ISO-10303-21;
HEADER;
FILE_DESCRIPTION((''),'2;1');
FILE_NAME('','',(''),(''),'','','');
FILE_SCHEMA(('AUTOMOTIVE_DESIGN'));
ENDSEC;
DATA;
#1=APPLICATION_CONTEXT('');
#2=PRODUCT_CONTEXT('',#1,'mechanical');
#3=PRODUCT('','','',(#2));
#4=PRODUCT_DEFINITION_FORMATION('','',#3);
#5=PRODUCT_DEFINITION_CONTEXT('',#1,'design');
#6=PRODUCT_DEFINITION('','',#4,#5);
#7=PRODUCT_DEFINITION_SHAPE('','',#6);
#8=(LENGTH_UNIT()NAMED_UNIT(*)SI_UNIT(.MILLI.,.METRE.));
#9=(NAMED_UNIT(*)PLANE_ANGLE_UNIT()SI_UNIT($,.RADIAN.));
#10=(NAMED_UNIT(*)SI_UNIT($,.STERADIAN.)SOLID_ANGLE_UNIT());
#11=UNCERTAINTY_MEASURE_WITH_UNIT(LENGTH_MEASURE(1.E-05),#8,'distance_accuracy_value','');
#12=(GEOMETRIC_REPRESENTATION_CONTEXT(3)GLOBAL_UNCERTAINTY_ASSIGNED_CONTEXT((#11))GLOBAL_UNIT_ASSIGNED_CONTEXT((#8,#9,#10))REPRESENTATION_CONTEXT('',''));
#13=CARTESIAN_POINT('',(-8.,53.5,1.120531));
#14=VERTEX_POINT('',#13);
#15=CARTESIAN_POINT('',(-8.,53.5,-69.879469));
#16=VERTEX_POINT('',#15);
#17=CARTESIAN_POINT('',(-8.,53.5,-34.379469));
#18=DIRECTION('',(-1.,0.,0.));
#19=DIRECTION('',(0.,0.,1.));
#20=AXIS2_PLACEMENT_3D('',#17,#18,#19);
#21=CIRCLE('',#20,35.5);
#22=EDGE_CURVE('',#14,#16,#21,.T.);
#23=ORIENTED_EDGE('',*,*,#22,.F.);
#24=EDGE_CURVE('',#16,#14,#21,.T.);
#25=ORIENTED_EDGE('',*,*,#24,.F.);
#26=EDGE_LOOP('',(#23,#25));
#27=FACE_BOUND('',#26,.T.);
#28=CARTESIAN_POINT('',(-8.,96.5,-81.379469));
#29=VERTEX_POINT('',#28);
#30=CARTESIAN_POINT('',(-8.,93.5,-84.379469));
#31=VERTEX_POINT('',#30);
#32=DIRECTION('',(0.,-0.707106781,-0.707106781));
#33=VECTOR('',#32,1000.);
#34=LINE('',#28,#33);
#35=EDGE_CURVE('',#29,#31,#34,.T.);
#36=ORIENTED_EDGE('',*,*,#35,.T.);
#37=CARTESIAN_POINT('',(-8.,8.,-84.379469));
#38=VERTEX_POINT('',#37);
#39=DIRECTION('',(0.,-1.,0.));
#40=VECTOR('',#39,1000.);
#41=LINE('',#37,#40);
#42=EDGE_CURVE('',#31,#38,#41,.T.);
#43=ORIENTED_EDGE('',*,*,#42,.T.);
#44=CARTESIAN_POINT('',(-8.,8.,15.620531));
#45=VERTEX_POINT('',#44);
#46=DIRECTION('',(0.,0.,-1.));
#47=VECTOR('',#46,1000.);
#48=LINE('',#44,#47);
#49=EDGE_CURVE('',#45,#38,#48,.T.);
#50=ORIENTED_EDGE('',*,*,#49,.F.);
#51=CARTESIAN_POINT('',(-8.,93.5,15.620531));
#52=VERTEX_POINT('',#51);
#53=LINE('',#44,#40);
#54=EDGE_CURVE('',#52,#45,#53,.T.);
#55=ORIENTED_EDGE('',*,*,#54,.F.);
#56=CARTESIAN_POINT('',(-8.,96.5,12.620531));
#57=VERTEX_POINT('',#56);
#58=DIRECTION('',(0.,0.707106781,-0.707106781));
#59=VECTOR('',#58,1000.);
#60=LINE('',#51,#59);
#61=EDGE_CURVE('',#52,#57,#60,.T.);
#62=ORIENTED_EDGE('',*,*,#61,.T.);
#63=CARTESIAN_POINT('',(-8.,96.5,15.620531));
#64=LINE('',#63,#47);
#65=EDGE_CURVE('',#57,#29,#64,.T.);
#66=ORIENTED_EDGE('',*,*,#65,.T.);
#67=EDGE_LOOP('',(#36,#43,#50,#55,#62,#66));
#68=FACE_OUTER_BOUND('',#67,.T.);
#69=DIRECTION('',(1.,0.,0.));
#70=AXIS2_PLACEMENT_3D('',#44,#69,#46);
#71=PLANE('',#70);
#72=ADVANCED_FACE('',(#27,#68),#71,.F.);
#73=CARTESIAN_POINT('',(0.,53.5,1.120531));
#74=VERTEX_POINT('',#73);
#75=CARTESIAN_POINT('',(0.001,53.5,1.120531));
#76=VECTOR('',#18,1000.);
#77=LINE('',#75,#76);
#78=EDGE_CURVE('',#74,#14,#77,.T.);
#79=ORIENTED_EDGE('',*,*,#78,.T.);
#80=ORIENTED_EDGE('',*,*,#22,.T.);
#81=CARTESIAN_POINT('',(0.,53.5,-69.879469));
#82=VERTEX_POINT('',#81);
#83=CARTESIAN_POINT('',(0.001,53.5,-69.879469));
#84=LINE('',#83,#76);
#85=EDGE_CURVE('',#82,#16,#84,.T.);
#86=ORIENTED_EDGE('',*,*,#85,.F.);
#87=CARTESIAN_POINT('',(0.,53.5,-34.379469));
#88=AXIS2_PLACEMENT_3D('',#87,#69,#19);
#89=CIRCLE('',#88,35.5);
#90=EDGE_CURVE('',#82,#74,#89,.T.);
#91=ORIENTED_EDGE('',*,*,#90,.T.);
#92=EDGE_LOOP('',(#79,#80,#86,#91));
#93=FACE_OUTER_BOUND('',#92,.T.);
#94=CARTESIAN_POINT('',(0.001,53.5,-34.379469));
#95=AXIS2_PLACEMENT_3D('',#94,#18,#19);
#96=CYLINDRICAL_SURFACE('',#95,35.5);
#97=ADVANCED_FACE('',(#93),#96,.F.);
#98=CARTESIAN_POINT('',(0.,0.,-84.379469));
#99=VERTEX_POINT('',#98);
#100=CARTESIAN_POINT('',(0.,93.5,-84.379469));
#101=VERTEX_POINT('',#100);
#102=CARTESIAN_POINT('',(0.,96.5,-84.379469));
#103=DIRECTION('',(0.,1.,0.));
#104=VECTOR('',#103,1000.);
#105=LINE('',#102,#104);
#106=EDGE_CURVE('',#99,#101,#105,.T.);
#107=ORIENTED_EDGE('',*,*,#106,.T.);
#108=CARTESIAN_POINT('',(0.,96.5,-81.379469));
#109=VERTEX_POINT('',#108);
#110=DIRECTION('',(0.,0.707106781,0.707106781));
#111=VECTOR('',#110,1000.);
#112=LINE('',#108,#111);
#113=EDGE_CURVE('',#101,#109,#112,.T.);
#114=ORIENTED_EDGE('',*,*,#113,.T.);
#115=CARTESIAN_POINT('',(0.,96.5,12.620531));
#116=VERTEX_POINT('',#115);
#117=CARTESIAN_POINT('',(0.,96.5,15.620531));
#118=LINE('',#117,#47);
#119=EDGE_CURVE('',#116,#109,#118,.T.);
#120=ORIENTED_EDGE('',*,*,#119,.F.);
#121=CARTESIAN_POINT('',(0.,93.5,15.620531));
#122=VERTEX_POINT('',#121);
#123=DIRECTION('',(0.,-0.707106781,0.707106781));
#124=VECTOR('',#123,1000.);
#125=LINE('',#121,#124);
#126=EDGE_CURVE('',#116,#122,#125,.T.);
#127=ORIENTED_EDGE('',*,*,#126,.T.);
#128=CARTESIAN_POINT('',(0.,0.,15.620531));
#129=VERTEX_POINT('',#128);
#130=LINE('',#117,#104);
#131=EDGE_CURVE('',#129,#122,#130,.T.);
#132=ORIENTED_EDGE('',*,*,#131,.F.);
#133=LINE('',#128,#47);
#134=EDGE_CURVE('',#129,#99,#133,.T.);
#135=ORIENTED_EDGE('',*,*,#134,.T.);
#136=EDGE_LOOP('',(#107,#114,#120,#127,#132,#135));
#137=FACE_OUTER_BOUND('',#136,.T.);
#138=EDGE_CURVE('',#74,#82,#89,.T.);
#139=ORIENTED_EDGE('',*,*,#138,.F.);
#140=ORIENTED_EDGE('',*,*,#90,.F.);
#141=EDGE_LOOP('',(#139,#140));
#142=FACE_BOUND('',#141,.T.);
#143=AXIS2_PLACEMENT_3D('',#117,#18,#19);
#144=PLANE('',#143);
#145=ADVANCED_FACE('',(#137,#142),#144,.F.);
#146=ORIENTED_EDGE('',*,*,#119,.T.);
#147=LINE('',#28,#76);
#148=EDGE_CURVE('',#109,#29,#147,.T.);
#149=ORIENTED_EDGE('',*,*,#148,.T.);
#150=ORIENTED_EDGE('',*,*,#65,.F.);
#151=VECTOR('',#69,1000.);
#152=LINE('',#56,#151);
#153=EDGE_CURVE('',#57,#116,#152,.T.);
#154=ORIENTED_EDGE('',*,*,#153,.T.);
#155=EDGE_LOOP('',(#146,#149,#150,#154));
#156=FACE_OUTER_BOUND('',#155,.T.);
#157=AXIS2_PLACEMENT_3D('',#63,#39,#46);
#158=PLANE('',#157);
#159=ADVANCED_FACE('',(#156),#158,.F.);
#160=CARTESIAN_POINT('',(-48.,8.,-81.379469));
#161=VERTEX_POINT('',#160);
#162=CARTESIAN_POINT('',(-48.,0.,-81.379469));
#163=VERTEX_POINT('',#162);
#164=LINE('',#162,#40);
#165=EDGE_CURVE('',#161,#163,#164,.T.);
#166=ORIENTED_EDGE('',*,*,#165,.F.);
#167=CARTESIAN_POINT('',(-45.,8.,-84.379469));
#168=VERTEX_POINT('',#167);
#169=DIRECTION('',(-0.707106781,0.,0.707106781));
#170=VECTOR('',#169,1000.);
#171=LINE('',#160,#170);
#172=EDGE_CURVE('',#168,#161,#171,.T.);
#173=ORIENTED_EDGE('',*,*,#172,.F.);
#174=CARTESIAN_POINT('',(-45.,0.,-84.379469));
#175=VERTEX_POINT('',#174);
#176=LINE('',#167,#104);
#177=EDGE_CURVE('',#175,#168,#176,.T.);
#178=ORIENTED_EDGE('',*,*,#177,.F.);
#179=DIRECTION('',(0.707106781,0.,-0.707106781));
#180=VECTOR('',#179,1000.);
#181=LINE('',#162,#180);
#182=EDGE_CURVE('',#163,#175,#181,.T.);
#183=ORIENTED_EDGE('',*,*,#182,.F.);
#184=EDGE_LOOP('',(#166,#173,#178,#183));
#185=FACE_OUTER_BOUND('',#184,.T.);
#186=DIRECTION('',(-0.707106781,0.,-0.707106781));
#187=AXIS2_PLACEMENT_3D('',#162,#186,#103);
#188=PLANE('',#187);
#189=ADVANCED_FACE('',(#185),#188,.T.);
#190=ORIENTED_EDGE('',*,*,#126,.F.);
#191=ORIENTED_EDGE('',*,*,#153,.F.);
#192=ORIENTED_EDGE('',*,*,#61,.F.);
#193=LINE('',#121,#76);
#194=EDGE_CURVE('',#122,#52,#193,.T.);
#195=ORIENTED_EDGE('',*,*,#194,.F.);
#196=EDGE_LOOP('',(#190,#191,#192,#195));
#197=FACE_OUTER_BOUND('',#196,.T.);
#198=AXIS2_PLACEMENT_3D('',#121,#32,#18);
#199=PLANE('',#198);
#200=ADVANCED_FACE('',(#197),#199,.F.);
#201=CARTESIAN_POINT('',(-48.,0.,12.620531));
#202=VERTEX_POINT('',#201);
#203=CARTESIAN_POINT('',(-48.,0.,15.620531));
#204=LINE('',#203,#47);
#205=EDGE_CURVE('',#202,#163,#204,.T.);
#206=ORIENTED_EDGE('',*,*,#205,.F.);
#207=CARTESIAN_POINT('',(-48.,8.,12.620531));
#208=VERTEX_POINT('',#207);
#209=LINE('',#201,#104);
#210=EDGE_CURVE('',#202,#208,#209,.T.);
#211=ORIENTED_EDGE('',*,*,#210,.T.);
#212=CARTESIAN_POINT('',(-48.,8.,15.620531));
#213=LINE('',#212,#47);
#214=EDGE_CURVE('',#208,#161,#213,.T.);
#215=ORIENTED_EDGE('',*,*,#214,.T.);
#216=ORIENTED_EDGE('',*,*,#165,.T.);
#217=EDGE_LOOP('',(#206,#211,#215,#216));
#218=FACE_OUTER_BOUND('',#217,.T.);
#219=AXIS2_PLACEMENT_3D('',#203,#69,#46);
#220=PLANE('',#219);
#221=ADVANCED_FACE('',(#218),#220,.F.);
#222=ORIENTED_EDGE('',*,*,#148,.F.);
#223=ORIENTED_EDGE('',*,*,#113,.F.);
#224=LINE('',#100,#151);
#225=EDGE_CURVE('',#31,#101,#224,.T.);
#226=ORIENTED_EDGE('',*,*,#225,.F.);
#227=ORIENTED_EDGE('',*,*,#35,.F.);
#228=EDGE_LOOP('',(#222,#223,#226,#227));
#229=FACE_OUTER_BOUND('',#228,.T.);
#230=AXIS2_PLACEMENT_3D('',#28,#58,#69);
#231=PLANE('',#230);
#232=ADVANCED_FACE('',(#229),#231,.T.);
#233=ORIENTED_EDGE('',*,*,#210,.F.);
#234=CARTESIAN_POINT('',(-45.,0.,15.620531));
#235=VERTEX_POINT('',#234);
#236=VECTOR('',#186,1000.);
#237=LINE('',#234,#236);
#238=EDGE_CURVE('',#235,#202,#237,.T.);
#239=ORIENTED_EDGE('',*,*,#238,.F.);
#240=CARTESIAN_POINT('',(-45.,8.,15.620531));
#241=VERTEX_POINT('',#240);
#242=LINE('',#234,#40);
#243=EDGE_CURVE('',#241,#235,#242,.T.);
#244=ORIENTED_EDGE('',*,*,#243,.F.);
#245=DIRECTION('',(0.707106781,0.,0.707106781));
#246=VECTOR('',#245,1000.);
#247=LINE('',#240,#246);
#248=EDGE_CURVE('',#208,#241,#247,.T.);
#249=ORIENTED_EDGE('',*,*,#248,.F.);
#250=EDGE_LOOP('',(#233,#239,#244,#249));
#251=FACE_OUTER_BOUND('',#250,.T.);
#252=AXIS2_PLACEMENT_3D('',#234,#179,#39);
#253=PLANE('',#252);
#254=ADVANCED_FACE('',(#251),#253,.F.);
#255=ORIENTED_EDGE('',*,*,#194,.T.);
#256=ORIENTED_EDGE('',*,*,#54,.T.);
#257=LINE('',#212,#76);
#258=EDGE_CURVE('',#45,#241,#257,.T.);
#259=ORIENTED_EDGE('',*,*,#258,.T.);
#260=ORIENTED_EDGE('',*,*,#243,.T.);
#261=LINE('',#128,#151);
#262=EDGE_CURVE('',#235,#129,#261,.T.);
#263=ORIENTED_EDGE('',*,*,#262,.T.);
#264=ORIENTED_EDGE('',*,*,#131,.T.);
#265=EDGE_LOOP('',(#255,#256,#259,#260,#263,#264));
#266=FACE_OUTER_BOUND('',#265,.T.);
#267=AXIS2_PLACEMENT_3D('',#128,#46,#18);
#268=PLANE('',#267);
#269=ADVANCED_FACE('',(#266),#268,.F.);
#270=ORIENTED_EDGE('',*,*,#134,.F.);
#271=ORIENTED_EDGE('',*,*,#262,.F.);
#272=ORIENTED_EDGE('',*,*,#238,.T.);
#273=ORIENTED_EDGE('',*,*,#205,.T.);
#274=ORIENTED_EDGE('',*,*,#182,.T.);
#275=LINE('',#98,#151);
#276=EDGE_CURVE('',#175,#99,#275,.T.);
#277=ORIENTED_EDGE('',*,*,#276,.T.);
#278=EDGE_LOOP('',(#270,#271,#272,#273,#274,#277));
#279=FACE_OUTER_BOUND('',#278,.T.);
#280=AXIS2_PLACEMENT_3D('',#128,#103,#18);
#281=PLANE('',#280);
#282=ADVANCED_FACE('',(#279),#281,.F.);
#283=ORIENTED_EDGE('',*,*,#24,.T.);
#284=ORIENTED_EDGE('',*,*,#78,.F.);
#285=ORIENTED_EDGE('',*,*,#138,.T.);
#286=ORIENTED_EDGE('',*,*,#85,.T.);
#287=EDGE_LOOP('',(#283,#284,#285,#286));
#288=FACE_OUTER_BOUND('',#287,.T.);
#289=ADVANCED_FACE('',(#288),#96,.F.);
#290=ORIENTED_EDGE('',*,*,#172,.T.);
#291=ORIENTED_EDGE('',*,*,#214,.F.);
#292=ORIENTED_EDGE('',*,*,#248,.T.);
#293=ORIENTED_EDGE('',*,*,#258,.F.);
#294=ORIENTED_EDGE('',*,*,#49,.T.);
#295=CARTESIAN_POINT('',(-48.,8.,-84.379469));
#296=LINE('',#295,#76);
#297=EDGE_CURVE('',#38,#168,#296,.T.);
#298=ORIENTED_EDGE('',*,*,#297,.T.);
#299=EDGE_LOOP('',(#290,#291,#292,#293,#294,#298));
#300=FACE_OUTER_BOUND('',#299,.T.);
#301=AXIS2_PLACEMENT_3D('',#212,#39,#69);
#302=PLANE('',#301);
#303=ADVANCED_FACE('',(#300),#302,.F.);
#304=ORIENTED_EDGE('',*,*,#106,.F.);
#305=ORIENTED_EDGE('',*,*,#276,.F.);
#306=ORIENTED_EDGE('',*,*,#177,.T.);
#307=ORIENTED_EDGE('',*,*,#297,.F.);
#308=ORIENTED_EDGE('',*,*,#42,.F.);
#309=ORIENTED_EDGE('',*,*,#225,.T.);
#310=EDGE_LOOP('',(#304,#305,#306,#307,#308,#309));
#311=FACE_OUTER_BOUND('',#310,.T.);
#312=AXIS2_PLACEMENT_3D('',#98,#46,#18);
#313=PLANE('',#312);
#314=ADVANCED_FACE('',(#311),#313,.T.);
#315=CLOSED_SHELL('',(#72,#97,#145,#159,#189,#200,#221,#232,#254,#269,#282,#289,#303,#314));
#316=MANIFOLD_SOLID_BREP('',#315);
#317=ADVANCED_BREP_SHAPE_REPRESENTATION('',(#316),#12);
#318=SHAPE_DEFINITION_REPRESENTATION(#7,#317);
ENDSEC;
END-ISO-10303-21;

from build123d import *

# Parameters (mm, degrees)
EXTRUDE_1_DEPTH     = 50
CHAMFER_1_SIZE      = 3
CUT_EXTRUDE_1_REACH = 136.284
SKETCH_4_R          = 35.5


with BuildPart() as part:
    # 草图2 → 凸台-拉伸1 (new, symmetric)
    with BuildSketch(Plane(origin=(409.637600706, 0.5, -34.379468655), x_dir=(1, 0, 0), z_dir=(0, 0, 1))):
        Polygon((-409.637600706, 96), (-409.637600706, -0.5), (-457.637600706, -0.5), (-457.637600706, 7.5), (-417.637600706, 7.5), (-417.637600706, 96), align=None)
    extrude(amount=EXTRUDE_1_DEPTH, both=True)

    # 倒角1
    chamfer_1_edges = [part.edges().sort_by_distance(p)[0] for p in [
        (-48, 4, 15.620531345),
        (-4, 96.5, 15.620531345),
        (-48, 4, -84.379468655),
        (-4, 96.5, -84.379468655),
    ]]
    chamfer(chamfer_1_edges, length=CHAMFER_1_SIZE)

    # 草图4 → 切除-拉伸1 (cut, up to next)
    with BuildSketch(Plane.ZY.offset(8), mode=Mode.PRIVATE) as cut_extrude_1_sk1:
        with Locations((-34.379468655, 53.5)):
            Circle(SKETCH_4_R)
    cut_extrude_1_tool1 = extrude(cut_extrude_1_sk1.sketch, amount=-CUT_EXTRUDE_1_REACH, mode=Mode.PRIVATE) & part.part
    add(cut_extrude_1_tool1.solids().sort_by_distance((-8, 53.5, -34.379469))[0], mode=Mode.SUBTRACT)


solid = part.part
